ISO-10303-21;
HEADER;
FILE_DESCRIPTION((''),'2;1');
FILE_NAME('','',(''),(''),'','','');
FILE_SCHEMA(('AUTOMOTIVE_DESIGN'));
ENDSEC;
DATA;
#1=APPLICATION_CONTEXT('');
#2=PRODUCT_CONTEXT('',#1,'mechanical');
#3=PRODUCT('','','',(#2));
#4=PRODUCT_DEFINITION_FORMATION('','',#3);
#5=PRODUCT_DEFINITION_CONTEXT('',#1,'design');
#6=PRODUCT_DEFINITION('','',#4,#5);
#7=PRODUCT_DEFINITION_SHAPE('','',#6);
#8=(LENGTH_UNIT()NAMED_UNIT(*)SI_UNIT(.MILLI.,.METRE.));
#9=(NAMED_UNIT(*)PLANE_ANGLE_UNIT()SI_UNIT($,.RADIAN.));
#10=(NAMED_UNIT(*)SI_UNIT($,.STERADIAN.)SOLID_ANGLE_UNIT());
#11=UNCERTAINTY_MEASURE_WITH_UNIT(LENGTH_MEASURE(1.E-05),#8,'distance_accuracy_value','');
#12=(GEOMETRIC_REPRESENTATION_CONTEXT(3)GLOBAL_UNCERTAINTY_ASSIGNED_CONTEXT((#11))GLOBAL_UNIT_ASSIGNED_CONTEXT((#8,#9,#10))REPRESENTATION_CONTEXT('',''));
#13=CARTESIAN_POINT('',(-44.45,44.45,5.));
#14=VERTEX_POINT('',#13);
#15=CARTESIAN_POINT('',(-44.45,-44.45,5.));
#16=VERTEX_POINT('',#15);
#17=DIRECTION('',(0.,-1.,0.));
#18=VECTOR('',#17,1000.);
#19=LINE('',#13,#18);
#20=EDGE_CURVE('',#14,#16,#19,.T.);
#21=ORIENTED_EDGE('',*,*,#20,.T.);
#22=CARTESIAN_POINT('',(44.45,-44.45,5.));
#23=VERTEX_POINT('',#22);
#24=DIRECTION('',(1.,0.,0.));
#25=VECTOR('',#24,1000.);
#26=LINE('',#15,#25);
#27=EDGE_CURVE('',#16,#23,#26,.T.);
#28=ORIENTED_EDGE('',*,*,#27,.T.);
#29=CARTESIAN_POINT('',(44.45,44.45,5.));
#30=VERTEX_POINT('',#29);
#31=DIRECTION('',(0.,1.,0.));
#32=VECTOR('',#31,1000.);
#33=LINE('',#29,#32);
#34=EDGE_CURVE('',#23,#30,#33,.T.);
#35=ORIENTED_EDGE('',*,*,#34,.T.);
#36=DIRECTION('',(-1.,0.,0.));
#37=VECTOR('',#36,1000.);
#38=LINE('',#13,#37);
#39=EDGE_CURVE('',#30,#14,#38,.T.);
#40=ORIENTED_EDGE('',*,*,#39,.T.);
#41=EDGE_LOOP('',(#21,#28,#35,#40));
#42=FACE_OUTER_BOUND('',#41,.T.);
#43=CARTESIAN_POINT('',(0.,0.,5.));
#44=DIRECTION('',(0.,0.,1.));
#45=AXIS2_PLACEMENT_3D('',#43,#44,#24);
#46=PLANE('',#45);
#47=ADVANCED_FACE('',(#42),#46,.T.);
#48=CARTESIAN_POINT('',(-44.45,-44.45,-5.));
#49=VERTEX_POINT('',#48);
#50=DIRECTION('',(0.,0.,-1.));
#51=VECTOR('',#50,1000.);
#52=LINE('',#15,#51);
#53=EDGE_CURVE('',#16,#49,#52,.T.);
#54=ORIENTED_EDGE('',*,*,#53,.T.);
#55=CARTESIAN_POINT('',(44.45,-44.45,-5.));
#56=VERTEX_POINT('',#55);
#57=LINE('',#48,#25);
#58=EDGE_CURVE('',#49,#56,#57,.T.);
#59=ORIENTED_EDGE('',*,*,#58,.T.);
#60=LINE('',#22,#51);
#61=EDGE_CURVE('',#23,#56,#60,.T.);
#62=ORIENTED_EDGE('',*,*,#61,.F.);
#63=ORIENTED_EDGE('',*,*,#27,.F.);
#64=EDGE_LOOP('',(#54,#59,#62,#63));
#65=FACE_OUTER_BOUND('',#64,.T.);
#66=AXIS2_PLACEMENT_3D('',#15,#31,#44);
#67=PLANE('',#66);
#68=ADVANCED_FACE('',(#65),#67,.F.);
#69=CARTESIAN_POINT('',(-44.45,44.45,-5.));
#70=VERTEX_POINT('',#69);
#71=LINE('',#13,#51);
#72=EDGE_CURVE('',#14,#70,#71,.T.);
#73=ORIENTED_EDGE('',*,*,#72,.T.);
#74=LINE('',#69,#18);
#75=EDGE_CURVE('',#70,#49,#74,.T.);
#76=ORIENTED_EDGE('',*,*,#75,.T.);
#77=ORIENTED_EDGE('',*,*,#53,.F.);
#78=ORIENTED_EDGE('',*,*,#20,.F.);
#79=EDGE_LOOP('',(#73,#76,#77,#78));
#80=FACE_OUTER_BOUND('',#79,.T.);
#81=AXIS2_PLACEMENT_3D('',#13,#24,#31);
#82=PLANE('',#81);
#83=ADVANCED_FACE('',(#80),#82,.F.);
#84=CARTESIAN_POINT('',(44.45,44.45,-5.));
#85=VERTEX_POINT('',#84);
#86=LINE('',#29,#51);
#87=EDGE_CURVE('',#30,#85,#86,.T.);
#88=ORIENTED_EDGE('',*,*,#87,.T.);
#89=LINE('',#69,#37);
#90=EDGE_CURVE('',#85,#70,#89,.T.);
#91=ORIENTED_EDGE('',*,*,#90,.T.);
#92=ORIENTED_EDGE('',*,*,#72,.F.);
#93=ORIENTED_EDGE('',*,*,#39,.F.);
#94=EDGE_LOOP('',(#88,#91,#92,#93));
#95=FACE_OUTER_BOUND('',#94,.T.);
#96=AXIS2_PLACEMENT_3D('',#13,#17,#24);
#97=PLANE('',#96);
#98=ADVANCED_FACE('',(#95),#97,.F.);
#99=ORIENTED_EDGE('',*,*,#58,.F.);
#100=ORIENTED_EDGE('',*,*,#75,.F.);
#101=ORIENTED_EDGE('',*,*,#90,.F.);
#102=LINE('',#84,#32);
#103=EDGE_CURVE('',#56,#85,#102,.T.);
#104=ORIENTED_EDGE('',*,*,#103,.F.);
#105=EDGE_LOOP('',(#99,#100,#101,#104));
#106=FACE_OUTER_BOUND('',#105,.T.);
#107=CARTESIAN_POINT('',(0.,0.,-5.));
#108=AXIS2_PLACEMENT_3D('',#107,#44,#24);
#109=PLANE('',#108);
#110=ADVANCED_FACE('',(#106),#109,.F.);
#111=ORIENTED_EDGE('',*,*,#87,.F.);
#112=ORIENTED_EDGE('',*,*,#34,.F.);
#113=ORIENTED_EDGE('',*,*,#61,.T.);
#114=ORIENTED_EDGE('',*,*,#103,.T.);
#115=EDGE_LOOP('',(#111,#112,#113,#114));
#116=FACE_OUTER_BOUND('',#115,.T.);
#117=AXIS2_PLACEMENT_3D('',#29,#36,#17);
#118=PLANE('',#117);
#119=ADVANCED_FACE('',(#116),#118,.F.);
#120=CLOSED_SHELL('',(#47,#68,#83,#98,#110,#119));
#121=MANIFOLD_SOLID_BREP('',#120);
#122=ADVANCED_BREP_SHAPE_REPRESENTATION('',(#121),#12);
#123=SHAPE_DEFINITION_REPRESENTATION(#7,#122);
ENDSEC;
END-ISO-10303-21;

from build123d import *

# Parameters (mm, degrees)
SKETCH1_W           = 88.9
SKETCH1_H           = 88.9
BOSS_EXTRUDE1_DEPTH = 5


with BuildPart() as part:
    # Sketch1 → Boss-Extrude1 (new, symmetric)
    with BuildSketch(Plane.XY):
        Rectangle(SKETCH1_W, SKETCH1_H)
    extrude(amount=BOSS_EXTRUDE1_DEPTH, both=True)


solid = part.part
